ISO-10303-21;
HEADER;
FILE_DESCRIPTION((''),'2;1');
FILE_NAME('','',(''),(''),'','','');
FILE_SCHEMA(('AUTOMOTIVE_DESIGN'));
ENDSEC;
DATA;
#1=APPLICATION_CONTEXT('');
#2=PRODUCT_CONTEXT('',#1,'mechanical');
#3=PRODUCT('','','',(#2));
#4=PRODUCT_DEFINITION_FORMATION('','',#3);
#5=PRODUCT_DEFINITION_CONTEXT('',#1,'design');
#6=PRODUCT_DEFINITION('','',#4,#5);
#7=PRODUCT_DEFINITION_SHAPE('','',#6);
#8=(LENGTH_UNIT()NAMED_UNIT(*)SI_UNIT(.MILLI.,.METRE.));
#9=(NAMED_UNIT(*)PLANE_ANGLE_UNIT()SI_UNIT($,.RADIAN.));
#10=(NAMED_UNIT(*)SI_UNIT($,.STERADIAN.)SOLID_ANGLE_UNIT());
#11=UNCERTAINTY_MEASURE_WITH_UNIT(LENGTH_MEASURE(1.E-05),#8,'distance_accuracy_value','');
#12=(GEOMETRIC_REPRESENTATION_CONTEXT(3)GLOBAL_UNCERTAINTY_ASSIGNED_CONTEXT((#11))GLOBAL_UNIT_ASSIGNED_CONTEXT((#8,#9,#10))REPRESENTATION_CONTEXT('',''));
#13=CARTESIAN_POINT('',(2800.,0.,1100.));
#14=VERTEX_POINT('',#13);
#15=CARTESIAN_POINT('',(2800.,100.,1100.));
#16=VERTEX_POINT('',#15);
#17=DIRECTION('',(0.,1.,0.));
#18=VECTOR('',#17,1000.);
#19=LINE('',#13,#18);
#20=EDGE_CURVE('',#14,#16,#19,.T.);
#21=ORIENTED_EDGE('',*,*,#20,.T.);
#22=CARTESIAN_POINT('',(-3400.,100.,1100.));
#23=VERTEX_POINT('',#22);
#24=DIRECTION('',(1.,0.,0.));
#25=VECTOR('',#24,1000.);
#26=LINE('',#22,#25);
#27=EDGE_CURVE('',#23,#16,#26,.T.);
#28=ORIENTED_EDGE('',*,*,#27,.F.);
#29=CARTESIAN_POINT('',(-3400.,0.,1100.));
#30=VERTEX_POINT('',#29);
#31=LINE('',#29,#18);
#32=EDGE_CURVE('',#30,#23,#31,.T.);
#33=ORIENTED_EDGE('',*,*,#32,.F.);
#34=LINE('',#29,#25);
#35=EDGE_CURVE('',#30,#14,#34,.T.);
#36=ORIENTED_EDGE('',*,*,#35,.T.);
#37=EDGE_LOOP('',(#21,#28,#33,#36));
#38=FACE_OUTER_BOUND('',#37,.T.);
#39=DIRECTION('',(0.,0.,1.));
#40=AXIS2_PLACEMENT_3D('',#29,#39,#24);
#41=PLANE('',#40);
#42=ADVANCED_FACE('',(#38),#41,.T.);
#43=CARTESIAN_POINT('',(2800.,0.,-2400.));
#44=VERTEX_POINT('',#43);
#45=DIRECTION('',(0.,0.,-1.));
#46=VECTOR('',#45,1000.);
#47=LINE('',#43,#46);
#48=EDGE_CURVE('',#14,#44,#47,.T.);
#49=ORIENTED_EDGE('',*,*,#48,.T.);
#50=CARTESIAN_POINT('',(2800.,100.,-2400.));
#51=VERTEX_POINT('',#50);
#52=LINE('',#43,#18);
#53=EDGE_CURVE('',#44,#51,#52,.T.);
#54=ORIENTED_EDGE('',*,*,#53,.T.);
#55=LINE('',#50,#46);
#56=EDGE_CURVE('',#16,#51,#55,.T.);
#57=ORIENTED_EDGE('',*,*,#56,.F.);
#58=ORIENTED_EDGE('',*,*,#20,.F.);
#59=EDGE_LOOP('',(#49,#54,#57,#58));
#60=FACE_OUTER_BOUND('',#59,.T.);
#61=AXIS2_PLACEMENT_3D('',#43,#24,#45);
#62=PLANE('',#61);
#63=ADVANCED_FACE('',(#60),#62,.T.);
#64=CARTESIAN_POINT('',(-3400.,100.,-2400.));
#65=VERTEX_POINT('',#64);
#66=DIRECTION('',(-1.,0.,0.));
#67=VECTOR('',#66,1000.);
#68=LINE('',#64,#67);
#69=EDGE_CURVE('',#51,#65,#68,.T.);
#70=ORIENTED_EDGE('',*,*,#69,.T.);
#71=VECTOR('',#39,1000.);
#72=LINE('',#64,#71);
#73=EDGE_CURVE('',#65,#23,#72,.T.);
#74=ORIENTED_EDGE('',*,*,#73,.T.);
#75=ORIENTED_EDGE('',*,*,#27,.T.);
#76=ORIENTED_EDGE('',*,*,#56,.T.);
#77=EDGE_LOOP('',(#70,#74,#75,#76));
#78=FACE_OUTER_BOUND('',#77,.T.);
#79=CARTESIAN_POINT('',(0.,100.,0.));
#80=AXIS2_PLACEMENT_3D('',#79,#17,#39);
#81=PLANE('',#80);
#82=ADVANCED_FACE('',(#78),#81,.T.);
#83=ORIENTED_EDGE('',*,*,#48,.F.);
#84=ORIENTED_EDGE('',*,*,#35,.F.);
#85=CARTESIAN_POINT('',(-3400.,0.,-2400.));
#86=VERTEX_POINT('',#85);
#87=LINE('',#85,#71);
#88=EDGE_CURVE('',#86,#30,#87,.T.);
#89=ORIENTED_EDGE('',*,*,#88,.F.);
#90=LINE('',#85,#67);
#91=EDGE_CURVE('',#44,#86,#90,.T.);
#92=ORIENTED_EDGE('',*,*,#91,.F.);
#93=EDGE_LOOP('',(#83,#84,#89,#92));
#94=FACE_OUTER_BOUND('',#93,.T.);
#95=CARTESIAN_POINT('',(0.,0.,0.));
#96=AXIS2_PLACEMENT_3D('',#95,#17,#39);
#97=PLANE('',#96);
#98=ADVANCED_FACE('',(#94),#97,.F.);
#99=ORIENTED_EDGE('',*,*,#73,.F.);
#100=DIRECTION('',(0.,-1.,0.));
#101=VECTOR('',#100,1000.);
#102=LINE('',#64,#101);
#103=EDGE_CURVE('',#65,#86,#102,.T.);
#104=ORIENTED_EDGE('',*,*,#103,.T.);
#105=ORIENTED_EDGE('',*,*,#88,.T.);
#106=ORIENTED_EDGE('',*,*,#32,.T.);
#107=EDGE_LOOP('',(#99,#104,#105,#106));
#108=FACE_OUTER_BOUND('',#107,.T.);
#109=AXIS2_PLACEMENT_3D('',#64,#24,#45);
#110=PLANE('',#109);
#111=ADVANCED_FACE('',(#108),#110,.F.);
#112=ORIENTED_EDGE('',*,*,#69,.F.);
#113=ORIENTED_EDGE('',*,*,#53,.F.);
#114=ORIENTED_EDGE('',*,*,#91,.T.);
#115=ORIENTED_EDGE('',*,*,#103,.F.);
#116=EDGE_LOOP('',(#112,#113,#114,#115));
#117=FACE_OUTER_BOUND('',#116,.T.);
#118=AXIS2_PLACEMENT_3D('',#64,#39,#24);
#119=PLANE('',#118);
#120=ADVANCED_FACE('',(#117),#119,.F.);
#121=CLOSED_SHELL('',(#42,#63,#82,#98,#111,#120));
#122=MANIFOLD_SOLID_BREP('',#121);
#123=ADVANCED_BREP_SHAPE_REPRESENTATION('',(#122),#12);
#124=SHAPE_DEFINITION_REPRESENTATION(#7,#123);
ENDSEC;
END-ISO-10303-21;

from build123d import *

# Parameters (mm, degrees)
SKETCH1_W           = 6800
SKETCH1_H           = 4800
BOSS_EXTRUDE1_DEPTH = 100
SKETCH2_OUTSIDE_W   = 8466.812
SKETCH2_OUTSIDE_H   = 6466.812
SKETCH2_OUTSIDE_W_2 = 6200
SKETCH2_OUTSIDE_H_2 = 3500
CUT_EXTRUDE1_DEPTH  = 4163.9316593


with BuildPart() as part:
    # Sketch1 → Boss-Extrude1 (new body)
    with BuildSketch(Plane(origin=(0, 0, 0), x_dir=(1, 0, 0), z_dir=(0, 1, 0))):
        Rectangle(SKETCH1_W, SKETCH1_H)
    extrude(amount=BOSS_EXTRUDE1_DEPTH)

    # Sketch2 outside → Cut-Extrude1 (cut, through all)
    with BuildSketch(Plane(origin=(0, 100, 0), x_dir=(1, 0, 0), z_dir=(0, 1, 0))):
        Rectangle(SKETCH2_OUTSIDE_W, SKETCH2_OUTSIDE_H)
        with Locations((-300, 650)):
            Rectangle(SKETCH2_OUTSIDE_W_2, SKETCH2_OUTSIDE_H_2, mode=Mode.SUBTRACT)
    extrude(amount=-CUT_EXTRUDE1_DEPTH, mode=Mode.SUBTRACT)


solid = part.part
